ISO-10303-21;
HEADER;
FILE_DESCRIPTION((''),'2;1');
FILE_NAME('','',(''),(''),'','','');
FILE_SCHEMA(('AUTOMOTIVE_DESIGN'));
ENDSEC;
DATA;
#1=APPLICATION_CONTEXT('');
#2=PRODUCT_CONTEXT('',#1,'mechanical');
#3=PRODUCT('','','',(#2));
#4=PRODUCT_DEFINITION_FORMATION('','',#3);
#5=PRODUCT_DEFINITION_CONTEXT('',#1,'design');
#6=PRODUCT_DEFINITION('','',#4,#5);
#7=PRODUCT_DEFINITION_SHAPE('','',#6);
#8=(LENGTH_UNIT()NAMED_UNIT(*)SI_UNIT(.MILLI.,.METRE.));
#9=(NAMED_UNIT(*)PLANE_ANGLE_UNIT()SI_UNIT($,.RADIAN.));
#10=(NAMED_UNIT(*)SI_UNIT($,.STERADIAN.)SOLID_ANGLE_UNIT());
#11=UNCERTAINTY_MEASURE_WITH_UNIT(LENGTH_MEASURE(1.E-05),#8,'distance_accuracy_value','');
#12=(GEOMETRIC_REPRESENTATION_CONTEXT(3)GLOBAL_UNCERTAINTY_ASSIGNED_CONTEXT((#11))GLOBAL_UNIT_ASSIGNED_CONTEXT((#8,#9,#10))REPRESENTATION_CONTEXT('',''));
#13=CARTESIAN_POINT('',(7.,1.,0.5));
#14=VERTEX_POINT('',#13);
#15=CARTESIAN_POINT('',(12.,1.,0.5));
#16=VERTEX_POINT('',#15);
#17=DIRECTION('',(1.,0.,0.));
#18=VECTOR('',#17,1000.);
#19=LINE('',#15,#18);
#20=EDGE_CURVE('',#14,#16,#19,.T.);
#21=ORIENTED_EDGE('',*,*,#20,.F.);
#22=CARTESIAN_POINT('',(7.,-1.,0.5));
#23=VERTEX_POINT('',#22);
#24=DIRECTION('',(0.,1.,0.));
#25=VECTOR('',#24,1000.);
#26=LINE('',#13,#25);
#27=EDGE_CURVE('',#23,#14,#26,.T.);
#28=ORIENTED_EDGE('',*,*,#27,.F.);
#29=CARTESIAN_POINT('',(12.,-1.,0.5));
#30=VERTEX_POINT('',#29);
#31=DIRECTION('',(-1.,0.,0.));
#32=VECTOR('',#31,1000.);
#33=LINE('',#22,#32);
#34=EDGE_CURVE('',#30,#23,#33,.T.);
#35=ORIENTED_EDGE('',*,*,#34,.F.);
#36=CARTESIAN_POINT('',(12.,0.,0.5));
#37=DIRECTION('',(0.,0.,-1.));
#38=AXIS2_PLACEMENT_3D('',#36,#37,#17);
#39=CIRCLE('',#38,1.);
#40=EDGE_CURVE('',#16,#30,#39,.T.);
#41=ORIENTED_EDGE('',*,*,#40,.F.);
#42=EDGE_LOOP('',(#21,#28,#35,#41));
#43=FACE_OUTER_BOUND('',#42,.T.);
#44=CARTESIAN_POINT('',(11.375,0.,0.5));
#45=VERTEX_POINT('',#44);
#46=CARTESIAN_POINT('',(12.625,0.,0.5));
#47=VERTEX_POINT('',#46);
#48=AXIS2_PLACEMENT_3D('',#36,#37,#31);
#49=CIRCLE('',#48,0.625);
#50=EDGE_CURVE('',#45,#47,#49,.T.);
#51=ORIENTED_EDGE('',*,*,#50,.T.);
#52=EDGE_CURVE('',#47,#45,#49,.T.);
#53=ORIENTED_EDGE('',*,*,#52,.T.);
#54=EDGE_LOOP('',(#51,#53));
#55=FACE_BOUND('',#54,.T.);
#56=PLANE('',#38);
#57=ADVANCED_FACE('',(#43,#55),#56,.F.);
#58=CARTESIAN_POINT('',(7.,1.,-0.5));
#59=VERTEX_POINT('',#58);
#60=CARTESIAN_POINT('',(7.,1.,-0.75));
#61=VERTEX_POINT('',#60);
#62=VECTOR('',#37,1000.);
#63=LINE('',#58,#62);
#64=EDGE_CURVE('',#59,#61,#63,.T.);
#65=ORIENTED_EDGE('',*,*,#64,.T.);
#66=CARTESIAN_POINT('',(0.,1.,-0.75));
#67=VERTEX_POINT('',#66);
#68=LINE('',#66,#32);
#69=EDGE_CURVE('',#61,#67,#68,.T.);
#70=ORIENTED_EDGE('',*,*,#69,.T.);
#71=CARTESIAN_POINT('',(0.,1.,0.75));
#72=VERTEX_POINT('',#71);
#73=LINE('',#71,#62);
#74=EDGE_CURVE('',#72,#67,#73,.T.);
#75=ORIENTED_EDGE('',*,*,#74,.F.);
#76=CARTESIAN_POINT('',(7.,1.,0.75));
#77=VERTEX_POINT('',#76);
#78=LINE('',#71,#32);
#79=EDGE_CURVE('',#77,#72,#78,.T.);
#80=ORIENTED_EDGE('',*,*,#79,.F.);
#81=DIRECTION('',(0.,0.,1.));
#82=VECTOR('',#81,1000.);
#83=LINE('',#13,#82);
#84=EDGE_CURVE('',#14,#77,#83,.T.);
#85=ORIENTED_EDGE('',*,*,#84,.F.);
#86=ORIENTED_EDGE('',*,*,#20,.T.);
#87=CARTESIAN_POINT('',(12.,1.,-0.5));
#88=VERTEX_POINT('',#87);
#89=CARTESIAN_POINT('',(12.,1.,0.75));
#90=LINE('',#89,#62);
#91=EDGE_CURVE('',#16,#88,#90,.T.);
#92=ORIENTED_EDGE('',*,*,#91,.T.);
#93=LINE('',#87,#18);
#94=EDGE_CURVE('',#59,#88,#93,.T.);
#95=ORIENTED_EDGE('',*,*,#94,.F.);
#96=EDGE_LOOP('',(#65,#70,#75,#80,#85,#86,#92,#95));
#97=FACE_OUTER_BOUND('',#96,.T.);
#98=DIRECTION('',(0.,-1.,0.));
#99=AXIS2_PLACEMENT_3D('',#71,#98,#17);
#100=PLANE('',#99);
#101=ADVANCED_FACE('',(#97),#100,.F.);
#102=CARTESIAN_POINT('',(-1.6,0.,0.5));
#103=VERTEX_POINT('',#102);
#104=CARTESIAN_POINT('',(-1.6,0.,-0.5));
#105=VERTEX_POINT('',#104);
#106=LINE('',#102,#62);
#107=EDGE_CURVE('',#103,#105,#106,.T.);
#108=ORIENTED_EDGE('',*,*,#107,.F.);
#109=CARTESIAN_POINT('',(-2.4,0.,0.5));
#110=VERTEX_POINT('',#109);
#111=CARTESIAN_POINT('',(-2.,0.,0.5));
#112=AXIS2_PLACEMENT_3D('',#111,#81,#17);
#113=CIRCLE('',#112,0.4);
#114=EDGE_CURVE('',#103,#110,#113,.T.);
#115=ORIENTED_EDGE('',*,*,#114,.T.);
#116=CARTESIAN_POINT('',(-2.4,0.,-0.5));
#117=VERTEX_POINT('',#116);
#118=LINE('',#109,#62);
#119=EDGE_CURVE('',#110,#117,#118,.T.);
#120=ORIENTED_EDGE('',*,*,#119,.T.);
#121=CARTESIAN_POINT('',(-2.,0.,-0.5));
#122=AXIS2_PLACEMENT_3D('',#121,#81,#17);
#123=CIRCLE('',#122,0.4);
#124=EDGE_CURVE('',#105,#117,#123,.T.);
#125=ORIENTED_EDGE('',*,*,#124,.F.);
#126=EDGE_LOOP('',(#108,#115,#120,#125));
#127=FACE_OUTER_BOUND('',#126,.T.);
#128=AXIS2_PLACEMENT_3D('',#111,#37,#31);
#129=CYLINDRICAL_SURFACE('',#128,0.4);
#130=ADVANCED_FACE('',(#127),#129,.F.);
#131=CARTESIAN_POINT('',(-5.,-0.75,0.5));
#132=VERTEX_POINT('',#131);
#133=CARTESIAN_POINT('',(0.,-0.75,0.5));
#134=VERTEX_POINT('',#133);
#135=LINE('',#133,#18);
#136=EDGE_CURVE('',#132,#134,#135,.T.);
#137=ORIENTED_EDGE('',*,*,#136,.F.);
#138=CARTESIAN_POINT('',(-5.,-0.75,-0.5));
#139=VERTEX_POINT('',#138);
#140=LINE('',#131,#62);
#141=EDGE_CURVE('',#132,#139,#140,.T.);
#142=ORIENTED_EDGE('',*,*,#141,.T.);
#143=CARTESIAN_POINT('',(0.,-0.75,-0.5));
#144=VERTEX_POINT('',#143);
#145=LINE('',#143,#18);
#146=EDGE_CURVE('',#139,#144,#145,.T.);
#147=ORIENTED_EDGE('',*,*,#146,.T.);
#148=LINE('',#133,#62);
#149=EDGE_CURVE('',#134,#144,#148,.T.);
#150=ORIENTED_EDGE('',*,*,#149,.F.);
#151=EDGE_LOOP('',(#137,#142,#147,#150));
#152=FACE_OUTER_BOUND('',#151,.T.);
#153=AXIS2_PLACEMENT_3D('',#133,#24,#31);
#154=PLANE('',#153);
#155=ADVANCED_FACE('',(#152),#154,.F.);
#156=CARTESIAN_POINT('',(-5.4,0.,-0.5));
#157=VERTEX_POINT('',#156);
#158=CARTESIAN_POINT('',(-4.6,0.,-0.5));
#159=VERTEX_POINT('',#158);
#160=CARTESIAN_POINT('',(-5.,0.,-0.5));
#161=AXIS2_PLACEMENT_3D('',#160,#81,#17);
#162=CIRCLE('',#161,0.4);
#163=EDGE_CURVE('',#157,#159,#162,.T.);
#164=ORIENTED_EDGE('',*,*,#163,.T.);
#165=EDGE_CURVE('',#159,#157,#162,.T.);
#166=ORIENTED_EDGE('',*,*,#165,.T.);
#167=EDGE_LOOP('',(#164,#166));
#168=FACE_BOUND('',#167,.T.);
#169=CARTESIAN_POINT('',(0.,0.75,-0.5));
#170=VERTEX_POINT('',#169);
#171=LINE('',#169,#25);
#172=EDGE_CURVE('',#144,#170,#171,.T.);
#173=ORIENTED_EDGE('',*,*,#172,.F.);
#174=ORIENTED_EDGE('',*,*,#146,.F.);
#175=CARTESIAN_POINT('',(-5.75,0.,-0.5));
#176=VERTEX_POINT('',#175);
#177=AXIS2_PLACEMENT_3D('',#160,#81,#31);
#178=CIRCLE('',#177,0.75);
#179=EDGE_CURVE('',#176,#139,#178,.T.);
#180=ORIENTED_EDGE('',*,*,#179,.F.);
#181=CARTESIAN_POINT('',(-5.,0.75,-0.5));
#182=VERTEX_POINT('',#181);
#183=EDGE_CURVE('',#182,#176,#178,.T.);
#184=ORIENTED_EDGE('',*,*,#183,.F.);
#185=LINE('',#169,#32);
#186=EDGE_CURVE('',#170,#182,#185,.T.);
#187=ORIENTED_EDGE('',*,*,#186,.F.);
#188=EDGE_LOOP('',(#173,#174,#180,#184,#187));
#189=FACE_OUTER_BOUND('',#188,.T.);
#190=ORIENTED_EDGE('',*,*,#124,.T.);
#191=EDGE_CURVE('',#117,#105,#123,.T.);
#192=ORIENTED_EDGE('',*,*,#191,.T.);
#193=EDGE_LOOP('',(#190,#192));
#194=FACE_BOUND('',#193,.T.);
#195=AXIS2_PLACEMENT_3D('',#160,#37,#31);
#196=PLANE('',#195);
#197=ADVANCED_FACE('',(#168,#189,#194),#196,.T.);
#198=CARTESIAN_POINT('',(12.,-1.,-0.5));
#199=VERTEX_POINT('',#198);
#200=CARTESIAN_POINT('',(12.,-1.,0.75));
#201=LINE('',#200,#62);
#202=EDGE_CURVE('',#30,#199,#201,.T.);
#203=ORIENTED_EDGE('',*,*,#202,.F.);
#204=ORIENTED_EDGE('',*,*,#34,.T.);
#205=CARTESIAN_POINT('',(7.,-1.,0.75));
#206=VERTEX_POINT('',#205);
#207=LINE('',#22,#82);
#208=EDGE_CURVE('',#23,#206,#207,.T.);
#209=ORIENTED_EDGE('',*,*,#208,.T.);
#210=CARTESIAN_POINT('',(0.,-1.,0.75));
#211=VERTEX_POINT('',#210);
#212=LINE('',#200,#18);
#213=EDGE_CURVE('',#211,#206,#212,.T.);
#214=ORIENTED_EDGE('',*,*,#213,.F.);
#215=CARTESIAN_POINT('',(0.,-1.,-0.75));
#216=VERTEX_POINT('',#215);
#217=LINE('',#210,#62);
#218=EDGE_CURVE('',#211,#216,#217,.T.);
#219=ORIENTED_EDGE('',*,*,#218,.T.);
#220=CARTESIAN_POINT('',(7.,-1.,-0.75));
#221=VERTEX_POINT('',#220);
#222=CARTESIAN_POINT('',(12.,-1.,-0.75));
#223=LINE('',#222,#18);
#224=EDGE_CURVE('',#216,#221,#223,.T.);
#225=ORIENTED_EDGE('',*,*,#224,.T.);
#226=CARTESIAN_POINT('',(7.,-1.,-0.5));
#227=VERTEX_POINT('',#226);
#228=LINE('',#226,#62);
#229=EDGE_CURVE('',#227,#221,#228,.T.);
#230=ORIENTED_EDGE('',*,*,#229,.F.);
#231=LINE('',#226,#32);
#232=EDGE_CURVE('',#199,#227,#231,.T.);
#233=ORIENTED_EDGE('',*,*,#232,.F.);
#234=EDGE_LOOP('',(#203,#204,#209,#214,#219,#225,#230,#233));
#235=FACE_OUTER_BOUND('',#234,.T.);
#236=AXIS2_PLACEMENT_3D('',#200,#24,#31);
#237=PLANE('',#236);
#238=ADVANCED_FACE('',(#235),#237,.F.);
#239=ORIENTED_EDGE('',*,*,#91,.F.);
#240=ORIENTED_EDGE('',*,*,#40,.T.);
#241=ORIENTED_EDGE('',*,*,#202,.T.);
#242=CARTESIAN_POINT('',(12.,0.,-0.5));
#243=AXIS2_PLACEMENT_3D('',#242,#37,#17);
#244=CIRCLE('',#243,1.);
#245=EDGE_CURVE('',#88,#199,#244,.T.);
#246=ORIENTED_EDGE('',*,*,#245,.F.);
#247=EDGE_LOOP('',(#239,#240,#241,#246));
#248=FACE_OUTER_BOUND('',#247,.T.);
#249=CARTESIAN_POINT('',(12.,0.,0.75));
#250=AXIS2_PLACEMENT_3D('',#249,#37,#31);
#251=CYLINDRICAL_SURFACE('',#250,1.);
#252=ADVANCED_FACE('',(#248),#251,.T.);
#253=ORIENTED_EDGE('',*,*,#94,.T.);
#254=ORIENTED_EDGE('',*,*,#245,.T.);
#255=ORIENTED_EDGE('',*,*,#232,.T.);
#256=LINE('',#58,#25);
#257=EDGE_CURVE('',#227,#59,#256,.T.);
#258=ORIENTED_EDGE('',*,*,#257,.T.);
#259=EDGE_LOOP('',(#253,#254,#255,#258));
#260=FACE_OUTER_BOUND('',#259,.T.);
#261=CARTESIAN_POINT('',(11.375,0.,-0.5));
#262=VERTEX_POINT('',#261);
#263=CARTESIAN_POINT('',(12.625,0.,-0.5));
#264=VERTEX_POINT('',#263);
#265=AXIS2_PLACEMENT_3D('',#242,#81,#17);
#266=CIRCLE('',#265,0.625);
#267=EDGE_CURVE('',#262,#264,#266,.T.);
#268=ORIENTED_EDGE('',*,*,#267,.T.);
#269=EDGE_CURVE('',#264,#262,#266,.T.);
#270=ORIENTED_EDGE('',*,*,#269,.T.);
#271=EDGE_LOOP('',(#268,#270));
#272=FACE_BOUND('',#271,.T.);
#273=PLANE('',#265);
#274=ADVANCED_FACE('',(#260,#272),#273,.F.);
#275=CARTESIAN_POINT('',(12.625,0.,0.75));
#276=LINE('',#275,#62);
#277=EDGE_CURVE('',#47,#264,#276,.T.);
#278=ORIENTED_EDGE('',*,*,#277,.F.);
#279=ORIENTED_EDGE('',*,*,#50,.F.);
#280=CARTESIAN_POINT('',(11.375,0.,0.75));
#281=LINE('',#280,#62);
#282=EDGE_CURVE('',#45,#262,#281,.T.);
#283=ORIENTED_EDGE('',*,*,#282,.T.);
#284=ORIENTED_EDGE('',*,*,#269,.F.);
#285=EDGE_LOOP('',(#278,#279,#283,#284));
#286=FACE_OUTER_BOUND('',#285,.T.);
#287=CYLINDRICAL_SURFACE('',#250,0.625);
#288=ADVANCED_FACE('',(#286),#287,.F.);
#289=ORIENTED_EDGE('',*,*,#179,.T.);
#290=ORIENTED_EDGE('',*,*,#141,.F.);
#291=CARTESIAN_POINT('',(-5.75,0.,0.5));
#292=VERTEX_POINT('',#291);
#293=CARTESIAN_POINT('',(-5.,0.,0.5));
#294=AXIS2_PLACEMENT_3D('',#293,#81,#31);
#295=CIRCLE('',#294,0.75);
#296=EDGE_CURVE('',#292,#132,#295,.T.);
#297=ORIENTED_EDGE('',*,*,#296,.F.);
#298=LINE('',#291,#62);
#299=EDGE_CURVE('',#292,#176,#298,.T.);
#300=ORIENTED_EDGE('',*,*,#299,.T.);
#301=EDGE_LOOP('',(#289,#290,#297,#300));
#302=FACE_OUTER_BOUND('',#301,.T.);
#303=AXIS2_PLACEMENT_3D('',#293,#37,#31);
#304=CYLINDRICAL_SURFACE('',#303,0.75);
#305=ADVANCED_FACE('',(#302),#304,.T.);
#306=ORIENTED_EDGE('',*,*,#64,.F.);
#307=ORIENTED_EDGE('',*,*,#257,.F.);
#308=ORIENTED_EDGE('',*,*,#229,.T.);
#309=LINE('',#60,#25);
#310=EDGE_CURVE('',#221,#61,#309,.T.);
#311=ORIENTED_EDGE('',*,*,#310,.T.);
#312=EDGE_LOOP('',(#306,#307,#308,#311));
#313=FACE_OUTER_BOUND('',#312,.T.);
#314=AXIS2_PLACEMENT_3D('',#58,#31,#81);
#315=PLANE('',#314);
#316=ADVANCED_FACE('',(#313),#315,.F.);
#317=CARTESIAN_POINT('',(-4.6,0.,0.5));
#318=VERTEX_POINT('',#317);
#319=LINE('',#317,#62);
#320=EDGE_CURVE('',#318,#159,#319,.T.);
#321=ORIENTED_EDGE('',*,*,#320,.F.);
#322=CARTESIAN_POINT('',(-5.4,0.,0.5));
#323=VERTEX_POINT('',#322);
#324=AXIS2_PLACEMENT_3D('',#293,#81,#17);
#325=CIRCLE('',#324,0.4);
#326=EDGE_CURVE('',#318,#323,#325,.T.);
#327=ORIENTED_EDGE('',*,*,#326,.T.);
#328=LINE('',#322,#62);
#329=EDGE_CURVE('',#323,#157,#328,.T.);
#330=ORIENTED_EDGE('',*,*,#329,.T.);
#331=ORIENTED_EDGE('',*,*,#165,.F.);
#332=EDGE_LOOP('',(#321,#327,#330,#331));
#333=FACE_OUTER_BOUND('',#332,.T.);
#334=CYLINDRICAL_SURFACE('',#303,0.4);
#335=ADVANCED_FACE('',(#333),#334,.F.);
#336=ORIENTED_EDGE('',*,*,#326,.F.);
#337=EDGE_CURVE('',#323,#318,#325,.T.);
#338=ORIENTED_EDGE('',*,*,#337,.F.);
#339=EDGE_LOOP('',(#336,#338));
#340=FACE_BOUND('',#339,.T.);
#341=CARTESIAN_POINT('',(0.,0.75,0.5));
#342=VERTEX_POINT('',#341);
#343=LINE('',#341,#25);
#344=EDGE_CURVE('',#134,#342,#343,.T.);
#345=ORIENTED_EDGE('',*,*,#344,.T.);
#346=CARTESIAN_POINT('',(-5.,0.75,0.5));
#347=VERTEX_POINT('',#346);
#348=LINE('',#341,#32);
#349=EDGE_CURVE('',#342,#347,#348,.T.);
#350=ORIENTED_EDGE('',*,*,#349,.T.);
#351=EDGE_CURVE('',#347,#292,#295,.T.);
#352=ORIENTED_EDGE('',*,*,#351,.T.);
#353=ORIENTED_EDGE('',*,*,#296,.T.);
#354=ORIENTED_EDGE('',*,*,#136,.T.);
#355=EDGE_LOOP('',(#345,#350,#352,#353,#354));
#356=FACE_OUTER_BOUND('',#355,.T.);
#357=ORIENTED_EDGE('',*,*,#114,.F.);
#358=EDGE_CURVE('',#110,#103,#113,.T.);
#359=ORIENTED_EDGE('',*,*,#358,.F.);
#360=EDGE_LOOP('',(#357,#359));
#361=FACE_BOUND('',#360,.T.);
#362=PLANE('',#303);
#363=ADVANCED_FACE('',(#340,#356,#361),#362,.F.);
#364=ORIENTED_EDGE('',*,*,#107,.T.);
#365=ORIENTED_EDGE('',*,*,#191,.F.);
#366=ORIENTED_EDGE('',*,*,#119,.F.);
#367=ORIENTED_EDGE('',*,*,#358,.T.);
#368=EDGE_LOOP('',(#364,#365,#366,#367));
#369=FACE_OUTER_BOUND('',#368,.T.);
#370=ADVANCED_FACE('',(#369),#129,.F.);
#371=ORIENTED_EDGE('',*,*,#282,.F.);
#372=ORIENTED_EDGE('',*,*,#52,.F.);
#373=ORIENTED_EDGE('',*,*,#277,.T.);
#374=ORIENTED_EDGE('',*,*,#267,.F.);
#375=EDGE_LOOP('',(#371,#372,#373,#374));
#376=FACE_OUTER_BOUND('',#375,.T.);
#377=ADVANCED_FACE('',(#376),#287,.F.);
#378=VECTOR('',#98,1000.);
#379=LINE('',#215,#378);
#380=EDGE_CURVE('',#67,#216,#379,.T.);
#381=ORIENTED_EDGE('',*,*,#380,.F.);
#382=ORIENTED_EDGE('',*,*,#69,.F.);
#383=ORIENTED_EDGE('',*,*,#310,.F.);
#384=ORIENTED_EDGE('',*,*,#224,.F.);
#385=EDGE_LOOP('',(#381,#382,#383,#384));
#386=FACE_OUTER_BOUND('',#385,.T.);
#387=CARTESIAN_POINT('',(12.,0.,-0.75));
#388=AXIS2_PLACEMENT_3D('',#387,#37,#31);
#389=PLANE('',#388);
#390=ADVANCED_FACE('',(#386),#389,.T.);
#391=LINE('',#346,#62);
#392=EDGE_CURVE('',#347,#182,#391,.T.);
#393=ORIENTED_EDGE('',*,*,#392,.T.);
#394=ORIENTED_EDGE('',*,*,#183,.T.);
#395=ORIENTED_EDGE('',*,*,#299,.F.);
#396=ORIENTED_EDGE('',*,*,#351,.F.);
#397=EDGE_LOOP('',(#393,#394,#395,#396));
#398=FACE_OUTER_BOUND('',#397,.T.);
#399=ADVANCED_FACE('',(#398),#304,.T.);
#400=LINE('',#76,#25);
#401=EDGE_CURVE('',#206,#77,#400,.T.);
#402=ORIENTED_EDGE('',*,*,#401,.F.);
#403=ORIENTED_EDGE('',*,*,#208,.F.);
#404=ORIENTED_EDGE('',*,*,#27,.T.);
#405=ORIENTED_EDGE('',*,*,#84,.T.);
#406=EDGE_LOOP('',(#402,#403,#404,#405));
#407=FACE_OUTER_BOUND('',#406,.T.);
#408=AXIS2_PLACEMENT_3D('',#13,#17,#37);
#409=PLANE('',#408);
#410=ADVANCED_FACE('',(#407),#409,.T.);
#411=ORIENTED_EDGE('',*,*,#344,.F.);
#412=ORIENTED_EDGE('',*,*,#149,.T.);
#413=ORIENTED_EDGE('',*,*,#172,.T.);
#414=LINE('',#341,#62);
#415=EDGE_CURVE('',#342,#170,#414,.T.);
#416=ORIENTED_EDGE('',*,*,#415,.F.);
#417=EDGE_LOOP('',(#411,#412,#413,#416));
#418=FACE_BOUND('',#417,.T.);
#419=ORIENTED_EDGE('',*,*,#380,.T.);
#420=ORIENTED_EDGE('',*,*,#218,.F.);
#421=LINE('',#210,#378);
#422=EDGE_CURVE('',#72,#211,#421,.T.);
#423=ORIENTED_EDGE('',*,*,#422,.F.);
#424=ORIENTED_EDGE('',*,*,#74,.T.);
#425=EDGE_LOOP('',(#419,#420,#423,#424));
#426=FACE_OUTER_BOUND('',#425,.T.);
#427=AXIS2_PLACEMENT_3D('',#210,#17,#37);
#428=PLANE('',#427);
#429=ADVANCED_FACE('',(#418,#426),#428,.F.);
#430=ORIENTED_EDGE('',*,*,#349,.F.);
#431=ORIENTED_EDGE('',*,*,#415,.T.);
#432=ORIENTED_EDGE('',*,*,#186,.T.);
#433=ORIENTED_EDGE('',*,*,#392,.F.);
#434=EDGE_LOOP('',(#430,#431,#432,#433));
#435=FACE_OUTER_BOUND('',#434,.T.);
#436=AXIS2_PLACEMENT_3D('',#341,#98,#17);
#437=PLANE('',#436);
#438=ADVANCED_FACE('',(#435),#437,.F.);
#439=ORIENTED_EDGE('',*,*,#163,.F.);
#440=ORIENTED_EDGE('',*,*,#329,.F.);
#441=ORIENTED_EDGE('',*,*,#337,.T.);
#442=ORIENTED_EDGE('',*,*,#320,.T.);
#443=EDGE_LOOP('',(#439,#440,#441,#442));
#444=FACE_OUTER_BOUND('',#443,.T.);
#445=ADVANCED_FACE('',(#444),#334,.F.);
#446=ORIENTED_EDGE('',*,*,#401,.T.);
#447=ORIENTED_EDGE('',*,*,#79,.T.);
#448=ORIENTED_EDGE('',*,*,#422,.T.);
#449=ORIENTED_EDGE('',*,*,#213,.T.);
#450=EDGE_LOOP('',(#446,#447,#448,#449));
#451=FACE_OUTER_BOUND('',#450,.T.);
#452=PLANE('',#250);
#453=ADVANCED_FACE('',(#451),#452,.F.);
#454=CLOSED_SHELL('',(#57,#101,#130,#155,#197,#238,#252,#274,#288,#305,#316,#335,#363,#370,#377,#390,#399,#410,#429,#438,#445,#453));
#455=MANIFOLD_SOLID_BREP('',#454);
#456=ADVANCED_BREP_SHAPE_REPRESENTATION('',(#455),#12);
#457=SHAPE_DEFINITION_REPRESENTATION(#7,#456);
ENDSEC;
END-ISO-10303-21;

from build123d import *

# Parameters (mm, degrees)
SKETCH1_R           = 0.625
BOSS_EXTRUDE1_DEPTH = 0.75
SKETCH3_R           = 0.4
BOSS_EXTRUDE3_DEPTH = 0.5
CUT_EXTRUDE1_START  = -0.25
CUT_EXTRUDE1_DEPTH  = 0.25


with BuildPart() as part:
    # Sketch1 → Boss-Extrude1 (new, symmetric)
    with BuildSketch(Plane.XY):
        with BuildLine():
            Line((0, -1), (0, 1))
            Line((0, 1), (12, 1))
            ThreePointArc((12, 1), (13, 0), (12, -1))
            Line((12, -1), (0, -1))
        make_face()
        with Locations((12, 0)):
            Circle(SKETCH1_R, mode=Mode.SUBTRACT)
    extrude(amount=BOSS_EXTRUDE1_DEPTH, both=True)

    # Sketch3 → Boss-Extrude3 (add, symmetric)
    with BuildSketch(Plane.XY):
        with BuildLine():
            Line((0, -0.75), (-5, -0.75))
            ThreePointArc((-5, -0.75), (-5.75, 0), (-5, 0.75))
            Line((-5, 0.75), (0, 0.75))
            Line((0, 0.75), (0, -0.75))
        make_face()
        with Locations((-5, 0)):
            Circle(SKETCH3_R, mode=Mode.SUBTRACT)
        with Locations((-2, 0)):
            Circle(SKETCH3_R, mode=Mode.SUBTRACT)
    extrude(amount=BOSS_EXTRUDE3_DEPTH, both=True)

    # Sketch6 → Cut-Extrude1 (cut)
    with BuildSketch(Plane(origin=(0, 0, -0.75), x_dir=(-1, 0, 0), z_dir=(0, 0, -1)).offset(CUT_EXTRUDE1_START)):
        with BuildLine():
            Line((-7, 1), (-7, -1))
            Line((-7, -1), (-12, -1))
            ThreePointArc((-12, -1), (-13, 0), (-12, 1))
            Line((-12, 1), (-7, 1))
        make_face()
    cut_extrude1 = extrude(amount=CUT_EXTRUDE1_DEPTH, mode=Mode.SUBTRACT)

    # Mirror1: Cut-Extrude1 across plane
    add(cut_extrude1.mirror(Plane.XY), mode=Mode.SUBTRACT)


solid = part.part
